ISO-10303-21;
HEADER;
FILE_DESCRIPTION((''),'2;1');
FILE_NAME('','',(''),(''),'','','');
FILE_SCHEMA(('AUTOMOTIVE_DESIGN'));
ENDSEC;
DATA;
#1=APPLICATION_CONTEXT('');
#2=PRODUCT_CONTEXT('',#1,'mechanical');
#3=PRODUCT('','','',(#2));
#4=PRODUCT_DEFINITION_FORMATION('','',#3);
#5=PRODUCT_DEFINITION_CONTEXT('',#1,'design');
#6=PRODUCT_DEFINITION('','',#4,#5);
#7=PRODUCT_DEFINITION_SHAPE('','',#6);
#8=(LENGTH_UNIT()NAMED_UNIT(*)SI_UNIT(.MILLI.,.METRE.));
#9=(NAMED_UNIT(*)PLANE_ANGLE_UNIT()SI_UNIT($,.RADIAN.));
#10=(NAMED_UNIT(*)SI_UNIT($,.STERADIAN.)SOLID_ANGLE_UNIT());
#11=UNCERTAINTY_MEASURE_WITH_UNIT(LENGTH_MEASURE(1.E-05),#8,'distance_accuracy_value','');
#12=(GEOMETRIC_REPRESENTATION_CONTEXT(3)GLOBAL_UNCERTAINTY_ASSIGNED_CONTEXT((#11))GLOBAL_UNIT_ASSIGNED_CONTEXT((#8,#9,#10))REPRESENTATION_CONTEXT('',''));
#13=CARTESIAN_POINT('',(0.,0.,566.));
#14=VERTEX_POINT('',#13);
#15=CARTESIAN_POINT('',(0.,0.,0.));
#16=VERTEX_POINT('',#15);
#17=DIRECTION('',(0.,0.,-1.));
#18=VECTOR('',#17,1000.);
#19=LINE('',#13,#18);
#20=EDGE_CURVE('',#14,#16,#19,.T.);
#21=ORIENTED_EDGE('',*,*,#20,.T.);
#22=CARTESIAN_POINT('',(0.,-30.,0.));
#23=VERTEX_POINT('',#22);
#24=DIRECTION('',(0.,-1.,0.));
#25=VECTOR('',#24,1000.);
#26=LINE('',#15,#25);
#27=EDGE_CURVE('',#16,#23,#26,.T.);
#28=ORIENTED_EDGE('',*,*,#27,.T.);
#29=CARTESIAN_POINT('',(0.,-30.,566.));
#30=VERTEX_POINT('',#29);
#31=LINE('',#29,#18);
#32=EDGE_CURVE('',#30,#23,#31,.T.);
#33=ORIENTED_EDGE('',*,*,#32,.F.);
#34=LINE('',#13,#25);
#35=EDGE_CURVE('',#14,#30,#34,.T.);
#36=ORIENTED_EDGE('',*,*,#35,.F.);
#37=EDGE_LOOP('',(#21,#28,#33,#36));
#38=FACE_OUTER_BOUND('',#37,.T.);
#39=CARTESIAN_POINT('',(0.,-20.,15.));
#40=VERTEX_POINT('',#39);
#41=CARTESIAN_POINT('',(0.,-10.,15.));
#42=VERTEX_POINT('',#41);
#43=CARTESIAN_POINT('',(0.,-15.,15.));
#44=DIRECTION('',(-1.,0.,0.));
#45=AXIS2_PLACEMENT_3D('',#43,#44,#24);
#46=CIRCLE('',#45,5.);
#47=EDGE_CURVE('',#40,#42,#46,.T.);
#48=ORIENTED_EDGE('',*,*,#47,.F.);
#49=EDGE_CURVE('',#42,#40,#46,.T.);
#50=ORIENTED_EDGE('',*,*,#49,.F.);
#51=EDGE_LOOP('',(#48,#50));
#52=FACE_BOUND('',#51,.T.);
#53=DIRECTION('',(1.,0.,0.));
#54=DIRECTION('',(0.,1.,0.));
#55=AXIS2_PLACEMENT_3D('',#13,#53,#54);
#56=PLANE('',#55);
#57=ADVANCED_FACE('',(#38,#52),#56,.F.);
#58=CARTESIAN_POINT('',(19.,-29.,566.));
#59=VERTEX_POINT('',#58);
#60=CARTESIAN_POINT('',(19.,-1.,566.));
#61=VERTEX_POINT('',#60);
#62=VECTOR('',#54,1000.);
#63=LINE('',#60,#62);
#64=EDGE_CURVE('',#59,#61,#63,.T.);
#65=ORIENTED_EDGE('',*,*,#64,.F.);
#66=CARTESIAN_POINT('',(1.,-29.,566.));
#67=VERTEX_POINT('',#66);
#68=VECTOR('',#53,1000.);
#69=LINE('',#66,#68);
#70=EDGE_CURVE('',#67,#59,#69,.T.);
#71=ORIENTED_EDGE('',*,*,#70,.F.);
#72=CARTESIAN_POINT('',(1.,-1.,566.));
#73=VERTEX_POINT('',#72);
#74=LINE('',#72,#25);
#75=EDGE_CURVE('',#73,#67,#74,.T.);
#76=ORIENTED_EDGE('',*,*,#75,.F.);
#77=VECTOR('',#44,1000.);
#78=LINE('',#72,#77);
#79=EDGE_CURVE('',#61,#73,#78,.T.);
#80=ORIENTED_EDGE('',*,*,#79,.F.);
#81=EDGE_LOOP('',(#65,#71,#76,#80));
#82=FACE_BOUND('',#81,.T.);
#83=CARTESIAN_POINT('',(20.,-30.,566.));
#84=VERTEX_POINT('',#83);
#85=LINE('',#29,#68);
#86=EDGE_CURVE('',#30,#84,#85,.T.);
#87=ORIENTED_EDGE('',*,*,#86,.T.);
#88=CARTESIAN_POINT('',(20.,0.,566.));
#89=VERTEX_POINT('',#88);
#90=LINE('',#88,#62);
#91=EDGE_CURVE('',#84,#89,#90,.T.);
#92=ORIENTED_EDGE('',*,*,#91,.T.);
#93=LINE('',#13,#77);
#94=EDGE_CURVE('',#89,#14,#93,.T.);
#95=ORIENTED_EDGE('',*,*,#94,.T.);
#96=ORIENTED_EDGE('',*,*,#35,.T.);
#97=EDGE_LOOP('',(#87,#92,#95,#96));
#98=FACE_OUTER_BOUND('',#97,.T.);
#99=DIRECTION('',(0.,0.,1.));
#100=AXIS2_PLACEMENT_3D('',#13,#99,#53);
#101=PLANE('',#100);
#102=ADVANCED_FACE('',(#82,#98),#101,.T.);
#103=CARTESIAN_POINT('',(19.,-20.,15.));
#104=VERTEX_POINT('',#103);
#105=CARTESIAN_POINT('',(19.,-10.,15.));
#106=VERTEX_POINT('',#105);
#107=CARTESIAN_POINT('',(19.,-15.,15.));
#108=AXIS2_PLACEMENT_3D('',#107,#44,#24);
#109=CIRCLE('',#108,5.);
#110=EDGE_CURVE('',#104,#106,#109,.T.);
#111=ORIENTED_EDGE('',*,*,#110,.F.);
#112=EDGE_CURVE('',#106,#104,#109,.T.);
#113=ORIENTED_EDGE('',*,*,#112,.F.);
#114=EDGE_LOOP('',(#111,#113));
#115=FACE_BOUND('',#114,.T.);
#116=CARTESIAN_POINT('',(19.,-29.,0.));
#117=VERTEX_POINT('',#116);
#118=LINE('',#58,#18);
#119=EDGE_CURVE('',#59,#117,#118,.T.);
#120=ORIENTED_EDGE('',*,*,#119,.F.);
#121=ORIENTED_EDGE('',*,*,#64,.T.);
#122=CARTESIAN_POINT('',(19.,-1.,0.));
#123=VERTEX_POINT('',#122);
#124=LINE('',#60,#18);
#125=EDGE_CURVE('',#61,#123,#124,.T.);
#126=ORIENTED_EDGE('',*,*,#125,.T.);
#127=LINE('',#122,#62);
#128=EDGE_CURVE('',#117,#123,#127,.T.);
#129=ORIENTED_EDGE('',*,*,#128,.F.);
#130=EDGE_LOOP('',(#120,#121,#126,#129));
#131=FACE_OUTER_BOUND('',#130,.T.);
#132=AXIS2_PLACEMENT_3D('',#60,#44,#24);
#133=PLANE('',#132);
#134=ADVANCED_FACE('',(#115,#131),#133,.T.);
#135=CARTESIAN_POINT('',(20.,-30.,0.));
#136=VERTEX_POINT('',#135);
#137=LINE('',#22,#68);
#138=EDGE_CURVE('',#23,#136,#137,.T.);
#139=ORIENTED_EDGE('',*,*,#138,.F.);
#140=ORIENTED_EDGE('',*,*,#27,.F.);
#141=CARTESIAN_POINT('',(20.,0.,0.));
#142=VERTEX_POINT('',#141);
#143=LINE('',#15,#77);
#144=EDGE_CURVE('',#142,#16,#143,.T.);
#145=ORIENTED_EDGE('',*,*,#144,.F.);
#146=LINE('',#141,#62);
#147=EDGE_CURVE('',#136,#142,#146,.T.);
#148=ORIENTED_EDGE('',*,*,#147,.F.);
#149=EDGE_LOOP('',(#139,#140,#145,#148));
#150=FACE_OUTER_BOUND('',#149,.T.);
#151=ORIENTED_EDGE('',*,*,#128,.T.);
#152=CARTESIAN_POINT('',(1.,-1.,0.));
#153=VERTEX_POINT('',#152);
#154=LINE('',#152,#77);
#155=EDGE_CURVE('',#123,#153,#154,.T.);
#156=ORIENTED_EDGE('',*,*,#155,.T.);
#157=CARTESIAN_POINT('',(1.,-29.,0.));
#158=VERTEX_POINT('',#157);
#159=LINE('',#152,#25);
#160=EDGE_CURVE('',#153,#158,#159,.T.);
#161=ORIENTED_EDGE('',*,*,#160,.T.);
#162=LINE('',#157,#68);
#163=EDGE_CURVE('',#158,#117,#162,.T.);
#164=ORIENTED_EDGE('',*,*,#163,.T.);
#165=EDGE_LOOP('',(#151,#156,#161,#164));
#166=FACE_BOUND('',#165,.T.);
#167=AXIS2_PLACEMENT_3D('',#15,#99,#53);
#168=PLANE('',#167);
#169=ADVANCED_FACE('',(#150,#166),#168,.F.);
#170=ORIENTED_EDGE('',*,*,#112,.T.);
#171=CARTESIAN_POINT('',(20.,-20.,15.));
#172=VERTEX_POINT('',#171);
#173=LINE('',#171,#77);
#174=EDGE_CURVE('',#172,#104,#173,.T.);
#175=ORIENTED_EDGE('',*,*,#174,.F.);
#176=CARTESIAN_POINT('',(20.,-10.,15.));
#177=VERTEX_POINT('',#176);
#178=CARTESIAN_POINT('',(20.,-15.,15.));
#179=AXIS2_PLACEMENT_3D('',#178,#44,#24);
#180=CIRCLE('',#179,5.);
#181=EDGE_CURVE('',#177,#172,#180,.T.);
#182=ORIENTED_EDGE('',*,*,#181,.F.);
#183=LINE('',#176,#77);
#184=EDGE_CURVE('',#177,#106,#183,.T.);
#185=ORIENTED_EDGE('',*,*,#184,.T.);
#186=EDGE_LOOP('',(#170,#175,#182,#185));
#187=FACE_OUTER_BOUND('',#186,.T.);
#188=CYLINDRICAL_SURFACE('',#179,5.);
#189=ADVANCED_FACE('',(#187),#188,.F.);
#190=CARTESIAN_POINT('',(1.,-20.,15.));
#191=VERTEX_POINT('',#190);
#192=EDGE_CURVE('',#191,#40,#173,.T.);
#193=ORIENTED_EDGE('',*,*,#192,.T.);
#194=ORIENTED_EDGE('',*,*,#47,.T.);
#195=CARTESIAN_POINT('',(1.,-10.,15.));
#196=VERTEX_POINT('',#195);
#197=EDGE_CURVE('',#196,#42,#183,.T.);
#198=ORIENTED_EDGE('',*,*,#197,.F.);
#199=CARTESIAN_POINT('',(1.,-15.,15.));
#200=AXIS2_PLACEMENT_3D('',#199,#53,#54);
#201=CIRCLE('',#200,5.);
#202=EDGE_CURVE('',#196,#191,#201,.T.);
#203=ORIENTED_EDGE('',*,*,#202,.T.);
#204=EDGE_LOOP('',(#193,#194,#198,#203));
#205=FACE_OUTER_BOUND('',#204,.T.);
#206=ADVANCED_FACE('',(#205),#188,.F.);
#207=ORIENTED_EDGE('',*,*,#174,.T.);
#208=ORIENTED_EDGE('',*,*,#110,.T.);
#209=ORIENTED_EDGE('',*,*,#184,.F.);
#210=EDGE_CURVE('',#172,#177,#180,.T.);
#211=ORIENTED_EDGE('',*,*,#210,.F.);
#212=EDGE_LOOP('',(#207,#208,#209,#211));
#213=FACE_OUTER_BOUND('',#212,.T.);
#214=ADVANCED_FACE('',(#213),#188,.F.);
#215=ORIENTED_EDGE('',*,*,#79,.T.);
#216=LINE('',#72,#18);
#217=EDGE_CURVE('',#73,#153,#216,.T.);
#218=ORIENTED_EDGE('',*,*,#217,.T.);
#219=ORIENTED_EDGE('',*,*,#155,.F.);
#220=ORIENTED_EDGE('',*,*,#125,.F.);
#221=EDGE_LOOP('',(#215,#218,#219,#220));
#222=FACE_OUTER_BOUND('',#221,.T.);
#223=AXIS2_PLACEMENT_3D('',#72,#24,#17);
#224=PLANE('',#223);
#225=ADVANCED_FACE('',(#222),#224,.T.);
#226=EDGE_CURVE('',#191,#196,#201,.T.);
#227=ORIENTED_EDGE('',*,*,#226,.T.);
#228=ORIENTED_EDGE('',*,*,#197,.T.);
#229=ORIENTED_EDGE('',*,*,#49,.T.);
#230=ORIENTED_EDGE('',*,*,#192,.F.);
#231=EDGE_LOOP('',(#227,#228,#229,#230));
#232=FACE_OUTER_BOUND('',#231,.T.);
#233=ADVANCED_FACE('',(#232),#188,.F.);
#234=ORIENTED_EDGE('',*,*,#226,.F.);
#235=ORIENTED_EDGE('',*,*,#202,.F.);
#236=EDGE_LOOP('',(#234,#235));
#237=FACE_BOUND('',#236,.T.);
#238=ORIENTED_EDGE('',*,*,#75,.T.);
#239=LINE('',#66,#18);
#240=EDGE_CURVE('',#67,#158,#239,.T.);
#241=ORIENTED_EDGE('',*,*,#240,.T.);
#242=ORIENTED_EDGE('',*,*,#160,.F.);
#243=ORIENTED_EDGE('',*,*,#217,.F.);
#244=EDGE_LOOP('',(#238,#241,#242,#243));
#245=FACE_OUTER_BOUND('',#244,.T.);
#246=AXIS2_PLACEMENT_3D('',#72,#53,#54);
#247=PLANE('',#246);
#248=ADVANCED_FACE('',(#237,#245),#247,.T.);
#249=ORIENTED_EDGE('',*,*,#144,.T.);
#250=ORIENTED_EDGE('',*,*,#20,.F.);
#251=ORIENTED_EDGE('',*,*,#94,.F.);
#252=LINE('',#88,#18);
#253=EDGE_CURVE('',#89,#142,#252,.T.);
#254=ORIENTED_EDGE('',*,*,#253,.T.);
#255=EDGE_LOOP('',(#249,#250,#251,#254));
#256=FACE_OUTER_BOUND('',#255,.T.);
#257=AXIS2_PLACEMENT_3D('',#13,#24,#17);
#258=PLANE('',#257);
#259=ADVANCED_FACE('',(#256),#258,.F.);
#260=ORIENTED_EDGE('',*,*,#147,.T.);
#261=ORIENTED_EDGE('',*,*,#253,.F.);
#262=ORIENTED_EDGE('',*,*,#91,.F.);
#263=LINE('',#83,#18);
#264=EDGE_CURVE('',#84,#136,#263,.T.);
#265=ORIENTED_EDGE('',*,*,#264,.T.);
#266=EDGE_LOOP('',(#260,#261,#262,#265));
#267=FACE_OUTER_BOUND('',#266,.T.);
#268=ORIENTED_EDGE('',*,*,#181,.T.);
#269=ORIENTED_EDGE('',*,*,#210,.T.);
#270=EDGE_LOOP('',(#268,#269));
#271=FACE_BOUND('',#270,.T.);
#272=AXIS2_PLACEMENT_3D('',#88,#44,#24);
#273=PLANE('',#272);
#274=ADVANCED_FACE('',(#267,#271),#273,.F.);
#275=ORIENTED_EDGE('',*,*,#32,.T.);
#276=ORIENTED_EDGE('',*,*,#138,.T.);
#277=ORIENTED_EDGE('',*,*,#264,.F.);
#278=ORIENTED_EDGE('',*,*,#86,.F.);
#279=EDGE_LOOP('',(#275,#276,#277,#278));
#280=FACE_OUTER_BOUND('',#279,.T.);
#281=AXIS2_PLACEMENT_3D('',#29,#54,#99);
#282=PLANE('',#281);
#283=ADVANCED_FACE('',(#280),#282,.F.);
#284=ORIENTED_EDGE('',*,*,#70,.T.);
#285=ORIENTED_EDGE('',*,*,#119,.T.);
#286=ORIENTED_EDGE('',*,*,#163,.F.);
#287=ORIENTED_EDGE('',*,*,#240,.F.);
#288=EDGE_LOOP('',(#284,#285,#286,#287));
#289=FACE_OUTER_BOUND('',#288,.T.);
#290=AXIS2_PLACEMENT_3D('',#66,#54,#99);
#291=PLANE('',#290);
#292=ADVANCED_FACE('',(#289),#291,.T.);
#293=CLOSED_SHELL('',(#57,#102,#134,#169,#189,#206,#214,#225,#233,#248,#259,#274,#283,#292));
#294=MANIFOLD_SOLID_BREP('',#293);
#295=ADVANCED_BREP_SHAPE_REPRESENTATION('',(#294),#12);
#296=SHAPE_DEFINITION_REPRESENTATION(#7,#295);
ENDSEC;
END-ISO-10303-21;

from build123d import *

# Parameters (mm, degrees)
SKETCH1_W           = 20
SKETCH1_H           = 30
SKETCH1_W_2         = 18
SKETCH1_H_2         = 28
BOSS_EXTRUDE1_DEPTH = 566
SKETCH4_R           = 5
CUT_EXTRUDE1_DEPTH  = 568.147247194


with BuildPart() as part:
    # Sketch1 → Boss-Extrude1 (new body)
    with BuildSketch(Plane.XY):
        with Locations((10, -15)):
            Rectangle(SKETCH1_W, SKETCH1_H)
        with Locations((10, -15)):
            Rectangle(SKETCH1_W_2, SKETCH1_H_2, mode=Mode.SUBTRACT)
    extrude(amount=BOSS_EXTRUDE1_DEPTH)

    # Sketch4 → Cut-Extrude1 (cut, through all)
    with BuildSketch(Plane.ZY):
        with Locations(Location((15, -15, 0), (0, 0, 270))):
            Circle(SKETCH4_R)
    extrude(amount=-CUT_EXTRUDE1_DEPTH, mode=Mode.SUBTRACT)


solid = part.part
